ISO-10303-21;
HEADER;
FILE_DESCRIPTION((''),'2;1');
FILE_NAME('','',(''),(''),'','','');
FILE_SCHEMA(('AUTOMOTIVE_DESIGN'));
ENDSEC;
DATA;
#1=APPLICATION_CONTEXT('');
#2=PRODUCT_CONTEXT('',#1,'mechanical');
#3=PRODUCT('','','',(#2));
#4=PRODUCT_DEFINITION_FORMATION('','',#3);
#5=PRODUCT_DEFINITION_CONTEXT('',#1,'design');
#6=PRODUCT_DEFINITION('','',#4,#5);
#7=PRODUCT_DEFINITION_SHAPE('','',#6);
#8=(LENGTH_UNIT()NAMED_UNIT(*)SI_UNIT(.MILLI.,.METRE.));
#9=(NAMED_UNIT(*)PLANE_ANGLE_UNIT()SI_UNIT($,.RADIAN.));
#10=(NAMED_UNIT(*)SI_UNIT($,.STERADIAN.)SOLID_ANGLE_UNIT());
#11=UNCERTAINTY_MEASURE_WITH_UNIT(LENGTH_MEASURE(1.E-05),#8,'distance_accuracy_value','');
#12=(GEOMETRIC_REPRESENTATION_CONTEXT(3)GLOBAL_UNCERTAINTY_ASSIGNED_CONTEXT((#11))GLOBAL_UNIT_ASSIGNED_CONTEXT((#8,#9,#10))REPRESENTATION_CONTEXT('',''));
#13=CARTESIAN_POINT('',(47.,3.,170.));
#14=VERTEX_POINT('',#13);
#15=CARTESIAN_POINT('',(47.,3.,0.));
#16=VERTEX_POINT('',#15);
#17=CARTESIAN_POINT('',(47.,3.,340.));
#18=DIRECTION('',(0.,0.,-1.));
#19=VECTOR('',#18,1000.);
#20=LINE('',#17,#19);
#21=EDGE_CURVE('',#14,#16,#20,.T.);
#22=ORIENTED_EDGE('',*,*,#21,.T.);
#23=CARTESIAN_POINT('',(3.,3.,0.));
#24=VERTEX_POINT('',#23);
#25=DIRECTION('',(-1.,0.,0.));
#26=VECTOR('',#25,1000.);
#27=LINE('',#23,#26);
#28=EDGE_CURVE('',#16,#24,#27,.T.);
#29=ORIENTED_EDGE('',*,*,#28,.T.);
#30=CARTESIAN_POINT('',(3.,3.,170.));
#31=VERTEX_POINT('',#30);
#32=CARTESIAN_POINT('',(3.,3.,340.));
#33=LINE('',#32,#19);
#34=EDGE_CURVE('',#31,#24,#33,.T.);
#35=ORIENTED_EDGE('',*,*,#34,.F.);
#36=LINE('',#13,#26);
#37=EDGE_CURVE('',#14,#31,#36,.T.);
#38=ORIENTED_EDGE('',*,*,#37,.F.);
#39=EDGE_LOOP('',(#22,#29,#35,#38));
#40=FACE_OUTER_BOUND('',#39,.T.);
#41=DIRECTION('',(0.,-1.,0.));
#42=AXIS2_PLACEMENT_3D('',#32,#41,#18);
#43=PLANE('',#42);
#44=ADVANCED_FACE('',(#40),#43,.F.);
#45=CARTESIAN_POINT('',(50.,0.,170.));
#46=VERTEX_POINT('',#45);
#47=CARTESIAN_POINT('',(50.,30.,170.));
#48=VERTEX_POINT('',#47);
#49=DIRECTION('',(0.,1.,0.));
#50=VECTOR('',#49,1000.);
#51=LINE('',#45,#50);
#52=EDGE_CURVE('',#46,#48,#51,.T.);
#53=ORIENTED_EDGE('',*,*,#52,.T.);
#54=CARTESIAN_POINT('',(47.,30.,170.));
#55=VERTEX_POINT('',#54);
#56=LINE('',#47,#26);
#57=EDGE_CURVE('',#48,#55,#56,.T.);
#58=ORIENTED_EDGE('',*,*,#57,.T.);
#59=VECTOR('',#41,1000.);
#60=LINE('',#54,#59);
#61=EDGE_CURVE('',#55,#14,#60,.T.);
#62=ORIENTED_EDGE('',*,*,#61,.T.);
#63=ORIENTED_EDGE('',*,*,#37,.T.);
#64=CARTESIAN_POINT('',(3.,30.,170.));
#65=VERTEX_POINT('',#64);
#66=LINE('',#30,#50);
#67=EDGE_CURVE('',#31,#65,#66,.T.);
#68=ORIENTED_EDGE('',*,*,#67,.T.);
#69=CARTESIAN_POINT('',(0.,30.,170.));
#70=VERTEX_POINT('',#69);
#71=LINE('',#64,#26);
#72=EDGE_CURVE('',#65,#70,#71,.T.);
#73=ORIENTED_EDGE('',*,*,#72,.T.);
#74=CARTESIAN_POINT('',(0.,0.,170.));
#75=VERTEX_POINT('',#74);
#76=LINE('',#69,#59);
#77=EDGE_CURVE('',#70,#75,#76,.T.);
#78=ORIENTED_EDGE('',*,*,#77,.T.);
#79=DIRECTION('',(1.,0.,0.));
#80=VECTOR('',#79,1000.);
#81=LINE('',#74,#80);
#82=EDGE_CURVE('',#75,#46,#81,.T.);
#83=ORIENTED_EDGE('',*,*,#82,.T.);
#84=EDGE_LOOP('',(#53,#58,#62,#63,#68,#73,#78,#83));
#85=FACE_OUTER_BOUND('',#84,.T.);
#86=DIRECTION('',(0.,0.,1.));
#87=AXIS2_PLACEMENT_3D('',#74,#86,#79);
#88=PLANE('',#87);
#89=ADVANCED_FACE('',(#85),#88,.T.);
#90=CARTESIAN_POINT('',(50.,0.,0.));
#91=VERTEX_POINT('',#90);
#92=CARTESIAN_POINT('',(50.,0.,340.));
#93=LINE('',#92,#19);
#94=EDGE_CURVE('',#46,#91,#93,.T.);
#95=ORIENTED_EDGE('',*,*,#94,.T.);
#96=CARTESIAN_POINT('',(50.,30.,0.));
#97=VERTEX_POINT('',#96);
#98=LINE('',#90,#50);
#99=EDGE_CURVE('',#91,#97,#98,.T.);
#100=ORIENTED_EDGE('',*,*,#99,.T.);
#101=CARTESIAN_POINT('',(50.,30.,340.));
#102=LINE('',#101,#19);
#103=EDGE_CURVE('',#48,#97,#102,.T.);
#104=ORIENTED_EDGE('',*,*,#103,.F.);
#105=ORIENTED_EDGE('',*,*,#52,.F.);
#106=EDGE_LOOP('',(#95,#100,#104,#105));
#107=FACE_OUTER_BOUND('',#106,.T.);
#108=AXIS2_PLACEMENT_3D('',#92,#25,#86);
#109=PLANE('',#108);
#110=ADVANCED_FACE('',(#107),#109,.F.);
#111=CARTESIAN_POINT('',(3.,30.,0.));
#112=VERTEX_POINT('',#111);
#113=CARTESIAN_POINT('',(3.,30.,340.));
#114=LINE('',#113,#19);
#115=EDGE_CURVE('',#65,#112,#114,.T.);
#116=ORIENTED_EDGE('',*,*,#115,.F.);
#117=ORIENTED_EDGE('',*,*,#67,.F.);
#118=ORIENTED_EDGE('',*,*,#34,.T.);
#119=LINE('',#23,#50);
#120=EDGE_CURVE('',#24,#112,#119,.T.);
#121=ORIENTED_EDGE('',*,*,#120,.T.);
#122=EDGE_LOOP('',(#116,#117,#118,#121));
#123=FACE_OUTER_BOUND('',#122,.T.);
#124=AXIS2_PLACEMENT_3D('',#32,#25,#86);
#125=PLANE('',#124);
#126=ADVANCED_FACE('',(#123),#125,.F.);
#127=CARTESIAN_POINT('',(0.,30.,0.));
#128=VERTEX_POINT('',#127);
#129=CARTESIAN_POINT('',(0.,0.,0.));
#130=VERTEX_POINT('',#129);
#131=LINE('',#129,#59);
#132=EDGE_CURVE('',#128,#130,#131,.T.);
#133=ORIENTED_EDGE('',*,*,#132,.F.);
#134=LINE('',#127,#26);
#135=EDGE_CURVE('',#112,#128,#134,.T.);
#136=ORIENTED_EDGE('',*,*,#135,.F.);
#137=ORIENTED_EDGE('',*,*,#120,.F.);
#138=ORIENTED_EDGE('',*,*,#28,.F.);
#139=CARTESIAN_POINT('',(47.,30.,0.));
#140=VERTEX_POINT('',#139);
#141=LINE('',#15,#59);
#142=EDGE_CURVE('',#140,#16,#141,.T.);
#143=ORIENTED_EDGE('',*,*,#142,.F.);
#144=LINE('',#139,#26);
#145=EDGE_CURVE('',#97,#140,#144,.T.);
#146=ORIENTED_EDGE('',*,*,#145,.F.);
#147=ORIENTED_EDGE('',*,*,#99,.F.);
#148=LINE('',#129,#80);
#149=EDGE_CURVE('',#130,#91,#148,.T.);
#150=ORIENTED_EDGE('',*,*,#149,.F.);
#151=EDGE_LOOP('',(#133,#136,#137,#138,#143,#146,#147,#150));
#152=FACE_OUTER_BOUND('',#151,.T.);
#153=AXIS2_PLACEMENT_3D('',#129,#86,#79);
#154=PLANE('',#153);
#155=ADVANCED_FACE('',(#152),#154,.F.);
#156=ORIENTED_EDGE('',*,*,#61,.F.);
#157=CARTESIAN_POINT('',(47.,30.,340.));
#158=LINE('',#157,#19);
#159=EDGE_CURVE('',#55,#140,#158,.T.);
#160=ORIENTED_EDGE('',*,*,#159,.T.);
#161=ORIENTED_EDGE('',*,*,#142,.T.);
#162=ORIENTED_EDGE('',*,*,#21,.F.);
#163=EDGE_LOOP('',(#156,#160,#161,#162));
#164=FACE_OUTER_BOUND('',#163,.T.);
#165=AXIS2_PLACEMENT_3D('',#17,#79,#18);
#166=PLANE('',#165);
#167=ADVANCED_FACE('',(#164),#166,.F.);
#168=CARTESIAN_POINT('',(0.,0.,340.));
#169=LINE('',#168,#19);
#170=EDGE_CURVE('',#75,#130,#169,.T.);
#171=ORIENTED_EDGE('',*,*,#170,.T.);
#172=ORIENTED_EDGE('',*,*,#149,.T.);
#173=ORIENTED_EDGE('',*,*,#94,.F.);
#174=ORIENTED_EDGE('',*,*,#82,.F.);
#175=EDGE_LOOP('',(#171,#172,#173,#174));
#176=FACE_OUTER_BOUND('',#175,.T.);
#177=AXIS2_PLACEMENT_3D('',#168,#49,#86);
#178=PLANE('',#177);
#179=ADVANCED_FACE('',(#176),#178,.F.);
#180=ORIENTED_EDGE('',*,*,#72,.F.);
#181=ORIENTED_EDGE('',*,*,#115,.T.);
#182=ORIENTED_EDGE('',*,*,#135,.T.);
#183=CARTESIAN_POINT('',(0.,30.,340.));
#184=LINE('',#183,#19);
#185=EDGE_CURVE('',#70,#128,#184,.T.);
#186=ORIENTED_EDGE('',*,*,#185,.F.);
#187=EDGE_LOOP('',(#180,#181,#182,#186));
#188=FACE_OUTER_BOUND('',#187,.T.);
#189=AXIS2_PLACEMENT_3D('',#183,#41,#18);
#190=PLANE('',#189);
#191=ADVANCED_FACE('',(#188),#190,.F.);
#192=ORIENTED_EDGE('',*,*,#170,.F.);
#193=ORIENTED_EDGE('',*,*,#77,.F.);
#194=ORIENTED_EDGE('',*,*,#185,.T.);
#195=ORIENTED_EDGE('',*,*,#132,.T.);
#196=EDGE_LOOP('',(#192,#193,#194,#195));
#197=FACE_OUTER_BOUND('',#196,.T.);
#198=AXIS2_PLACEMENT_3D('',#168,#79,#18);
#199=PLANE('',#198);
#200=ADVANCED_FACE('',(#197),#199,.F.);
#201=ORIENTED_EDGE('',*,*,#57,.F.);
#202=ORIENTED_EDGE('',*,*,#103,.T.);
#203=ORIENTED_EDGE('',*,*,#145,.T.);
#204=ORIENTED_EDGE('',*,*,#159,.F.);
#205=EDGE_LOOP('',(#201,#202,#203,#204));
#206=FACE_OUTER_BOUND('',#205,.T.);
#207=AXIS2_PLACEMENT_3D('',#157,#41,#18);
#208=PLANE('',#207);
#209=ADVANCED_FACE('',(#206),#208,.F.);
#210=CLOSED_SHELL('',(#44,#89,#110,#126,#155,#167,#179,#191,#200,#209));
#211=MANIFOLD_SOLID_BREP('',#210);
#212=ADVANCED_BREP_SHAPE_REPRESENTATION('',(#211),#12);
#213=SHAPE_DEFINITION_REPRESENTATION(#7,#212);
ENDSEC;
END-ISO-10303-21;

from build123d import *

# Parameters (mm, degrees)
EXTRUDE_1_DEPTH     = 340
CUT_EXTRUDE_1_DEPTH = 170


with BuildPart() as part:
    # 草图1 → 凸台-拉伸1 (new body)
    with BuildSketch(Plane.XY):
        Polygon((0, 0), (0, 30), (3, 30), (3, 3), (47, 3), (47, 30), (50, 30), (50, 0), align=None)
    extrude(amount=EXTRUDE_1_DEPTH)

    # 草图2 → 切除-拉伸1 (cut)
    with BuildSketch(Plane.XY.offset(340)):
        Polygon((0, 0), (50, 0), (50, 30), (47, 30), (47, 3), (3, 3), (3, 30), (0, 30), align=None)
    extrude(amount=-CUT_EXTRUDE_1_DEPTH, mode=Mode.SUBTRACT)


solid = part.part
